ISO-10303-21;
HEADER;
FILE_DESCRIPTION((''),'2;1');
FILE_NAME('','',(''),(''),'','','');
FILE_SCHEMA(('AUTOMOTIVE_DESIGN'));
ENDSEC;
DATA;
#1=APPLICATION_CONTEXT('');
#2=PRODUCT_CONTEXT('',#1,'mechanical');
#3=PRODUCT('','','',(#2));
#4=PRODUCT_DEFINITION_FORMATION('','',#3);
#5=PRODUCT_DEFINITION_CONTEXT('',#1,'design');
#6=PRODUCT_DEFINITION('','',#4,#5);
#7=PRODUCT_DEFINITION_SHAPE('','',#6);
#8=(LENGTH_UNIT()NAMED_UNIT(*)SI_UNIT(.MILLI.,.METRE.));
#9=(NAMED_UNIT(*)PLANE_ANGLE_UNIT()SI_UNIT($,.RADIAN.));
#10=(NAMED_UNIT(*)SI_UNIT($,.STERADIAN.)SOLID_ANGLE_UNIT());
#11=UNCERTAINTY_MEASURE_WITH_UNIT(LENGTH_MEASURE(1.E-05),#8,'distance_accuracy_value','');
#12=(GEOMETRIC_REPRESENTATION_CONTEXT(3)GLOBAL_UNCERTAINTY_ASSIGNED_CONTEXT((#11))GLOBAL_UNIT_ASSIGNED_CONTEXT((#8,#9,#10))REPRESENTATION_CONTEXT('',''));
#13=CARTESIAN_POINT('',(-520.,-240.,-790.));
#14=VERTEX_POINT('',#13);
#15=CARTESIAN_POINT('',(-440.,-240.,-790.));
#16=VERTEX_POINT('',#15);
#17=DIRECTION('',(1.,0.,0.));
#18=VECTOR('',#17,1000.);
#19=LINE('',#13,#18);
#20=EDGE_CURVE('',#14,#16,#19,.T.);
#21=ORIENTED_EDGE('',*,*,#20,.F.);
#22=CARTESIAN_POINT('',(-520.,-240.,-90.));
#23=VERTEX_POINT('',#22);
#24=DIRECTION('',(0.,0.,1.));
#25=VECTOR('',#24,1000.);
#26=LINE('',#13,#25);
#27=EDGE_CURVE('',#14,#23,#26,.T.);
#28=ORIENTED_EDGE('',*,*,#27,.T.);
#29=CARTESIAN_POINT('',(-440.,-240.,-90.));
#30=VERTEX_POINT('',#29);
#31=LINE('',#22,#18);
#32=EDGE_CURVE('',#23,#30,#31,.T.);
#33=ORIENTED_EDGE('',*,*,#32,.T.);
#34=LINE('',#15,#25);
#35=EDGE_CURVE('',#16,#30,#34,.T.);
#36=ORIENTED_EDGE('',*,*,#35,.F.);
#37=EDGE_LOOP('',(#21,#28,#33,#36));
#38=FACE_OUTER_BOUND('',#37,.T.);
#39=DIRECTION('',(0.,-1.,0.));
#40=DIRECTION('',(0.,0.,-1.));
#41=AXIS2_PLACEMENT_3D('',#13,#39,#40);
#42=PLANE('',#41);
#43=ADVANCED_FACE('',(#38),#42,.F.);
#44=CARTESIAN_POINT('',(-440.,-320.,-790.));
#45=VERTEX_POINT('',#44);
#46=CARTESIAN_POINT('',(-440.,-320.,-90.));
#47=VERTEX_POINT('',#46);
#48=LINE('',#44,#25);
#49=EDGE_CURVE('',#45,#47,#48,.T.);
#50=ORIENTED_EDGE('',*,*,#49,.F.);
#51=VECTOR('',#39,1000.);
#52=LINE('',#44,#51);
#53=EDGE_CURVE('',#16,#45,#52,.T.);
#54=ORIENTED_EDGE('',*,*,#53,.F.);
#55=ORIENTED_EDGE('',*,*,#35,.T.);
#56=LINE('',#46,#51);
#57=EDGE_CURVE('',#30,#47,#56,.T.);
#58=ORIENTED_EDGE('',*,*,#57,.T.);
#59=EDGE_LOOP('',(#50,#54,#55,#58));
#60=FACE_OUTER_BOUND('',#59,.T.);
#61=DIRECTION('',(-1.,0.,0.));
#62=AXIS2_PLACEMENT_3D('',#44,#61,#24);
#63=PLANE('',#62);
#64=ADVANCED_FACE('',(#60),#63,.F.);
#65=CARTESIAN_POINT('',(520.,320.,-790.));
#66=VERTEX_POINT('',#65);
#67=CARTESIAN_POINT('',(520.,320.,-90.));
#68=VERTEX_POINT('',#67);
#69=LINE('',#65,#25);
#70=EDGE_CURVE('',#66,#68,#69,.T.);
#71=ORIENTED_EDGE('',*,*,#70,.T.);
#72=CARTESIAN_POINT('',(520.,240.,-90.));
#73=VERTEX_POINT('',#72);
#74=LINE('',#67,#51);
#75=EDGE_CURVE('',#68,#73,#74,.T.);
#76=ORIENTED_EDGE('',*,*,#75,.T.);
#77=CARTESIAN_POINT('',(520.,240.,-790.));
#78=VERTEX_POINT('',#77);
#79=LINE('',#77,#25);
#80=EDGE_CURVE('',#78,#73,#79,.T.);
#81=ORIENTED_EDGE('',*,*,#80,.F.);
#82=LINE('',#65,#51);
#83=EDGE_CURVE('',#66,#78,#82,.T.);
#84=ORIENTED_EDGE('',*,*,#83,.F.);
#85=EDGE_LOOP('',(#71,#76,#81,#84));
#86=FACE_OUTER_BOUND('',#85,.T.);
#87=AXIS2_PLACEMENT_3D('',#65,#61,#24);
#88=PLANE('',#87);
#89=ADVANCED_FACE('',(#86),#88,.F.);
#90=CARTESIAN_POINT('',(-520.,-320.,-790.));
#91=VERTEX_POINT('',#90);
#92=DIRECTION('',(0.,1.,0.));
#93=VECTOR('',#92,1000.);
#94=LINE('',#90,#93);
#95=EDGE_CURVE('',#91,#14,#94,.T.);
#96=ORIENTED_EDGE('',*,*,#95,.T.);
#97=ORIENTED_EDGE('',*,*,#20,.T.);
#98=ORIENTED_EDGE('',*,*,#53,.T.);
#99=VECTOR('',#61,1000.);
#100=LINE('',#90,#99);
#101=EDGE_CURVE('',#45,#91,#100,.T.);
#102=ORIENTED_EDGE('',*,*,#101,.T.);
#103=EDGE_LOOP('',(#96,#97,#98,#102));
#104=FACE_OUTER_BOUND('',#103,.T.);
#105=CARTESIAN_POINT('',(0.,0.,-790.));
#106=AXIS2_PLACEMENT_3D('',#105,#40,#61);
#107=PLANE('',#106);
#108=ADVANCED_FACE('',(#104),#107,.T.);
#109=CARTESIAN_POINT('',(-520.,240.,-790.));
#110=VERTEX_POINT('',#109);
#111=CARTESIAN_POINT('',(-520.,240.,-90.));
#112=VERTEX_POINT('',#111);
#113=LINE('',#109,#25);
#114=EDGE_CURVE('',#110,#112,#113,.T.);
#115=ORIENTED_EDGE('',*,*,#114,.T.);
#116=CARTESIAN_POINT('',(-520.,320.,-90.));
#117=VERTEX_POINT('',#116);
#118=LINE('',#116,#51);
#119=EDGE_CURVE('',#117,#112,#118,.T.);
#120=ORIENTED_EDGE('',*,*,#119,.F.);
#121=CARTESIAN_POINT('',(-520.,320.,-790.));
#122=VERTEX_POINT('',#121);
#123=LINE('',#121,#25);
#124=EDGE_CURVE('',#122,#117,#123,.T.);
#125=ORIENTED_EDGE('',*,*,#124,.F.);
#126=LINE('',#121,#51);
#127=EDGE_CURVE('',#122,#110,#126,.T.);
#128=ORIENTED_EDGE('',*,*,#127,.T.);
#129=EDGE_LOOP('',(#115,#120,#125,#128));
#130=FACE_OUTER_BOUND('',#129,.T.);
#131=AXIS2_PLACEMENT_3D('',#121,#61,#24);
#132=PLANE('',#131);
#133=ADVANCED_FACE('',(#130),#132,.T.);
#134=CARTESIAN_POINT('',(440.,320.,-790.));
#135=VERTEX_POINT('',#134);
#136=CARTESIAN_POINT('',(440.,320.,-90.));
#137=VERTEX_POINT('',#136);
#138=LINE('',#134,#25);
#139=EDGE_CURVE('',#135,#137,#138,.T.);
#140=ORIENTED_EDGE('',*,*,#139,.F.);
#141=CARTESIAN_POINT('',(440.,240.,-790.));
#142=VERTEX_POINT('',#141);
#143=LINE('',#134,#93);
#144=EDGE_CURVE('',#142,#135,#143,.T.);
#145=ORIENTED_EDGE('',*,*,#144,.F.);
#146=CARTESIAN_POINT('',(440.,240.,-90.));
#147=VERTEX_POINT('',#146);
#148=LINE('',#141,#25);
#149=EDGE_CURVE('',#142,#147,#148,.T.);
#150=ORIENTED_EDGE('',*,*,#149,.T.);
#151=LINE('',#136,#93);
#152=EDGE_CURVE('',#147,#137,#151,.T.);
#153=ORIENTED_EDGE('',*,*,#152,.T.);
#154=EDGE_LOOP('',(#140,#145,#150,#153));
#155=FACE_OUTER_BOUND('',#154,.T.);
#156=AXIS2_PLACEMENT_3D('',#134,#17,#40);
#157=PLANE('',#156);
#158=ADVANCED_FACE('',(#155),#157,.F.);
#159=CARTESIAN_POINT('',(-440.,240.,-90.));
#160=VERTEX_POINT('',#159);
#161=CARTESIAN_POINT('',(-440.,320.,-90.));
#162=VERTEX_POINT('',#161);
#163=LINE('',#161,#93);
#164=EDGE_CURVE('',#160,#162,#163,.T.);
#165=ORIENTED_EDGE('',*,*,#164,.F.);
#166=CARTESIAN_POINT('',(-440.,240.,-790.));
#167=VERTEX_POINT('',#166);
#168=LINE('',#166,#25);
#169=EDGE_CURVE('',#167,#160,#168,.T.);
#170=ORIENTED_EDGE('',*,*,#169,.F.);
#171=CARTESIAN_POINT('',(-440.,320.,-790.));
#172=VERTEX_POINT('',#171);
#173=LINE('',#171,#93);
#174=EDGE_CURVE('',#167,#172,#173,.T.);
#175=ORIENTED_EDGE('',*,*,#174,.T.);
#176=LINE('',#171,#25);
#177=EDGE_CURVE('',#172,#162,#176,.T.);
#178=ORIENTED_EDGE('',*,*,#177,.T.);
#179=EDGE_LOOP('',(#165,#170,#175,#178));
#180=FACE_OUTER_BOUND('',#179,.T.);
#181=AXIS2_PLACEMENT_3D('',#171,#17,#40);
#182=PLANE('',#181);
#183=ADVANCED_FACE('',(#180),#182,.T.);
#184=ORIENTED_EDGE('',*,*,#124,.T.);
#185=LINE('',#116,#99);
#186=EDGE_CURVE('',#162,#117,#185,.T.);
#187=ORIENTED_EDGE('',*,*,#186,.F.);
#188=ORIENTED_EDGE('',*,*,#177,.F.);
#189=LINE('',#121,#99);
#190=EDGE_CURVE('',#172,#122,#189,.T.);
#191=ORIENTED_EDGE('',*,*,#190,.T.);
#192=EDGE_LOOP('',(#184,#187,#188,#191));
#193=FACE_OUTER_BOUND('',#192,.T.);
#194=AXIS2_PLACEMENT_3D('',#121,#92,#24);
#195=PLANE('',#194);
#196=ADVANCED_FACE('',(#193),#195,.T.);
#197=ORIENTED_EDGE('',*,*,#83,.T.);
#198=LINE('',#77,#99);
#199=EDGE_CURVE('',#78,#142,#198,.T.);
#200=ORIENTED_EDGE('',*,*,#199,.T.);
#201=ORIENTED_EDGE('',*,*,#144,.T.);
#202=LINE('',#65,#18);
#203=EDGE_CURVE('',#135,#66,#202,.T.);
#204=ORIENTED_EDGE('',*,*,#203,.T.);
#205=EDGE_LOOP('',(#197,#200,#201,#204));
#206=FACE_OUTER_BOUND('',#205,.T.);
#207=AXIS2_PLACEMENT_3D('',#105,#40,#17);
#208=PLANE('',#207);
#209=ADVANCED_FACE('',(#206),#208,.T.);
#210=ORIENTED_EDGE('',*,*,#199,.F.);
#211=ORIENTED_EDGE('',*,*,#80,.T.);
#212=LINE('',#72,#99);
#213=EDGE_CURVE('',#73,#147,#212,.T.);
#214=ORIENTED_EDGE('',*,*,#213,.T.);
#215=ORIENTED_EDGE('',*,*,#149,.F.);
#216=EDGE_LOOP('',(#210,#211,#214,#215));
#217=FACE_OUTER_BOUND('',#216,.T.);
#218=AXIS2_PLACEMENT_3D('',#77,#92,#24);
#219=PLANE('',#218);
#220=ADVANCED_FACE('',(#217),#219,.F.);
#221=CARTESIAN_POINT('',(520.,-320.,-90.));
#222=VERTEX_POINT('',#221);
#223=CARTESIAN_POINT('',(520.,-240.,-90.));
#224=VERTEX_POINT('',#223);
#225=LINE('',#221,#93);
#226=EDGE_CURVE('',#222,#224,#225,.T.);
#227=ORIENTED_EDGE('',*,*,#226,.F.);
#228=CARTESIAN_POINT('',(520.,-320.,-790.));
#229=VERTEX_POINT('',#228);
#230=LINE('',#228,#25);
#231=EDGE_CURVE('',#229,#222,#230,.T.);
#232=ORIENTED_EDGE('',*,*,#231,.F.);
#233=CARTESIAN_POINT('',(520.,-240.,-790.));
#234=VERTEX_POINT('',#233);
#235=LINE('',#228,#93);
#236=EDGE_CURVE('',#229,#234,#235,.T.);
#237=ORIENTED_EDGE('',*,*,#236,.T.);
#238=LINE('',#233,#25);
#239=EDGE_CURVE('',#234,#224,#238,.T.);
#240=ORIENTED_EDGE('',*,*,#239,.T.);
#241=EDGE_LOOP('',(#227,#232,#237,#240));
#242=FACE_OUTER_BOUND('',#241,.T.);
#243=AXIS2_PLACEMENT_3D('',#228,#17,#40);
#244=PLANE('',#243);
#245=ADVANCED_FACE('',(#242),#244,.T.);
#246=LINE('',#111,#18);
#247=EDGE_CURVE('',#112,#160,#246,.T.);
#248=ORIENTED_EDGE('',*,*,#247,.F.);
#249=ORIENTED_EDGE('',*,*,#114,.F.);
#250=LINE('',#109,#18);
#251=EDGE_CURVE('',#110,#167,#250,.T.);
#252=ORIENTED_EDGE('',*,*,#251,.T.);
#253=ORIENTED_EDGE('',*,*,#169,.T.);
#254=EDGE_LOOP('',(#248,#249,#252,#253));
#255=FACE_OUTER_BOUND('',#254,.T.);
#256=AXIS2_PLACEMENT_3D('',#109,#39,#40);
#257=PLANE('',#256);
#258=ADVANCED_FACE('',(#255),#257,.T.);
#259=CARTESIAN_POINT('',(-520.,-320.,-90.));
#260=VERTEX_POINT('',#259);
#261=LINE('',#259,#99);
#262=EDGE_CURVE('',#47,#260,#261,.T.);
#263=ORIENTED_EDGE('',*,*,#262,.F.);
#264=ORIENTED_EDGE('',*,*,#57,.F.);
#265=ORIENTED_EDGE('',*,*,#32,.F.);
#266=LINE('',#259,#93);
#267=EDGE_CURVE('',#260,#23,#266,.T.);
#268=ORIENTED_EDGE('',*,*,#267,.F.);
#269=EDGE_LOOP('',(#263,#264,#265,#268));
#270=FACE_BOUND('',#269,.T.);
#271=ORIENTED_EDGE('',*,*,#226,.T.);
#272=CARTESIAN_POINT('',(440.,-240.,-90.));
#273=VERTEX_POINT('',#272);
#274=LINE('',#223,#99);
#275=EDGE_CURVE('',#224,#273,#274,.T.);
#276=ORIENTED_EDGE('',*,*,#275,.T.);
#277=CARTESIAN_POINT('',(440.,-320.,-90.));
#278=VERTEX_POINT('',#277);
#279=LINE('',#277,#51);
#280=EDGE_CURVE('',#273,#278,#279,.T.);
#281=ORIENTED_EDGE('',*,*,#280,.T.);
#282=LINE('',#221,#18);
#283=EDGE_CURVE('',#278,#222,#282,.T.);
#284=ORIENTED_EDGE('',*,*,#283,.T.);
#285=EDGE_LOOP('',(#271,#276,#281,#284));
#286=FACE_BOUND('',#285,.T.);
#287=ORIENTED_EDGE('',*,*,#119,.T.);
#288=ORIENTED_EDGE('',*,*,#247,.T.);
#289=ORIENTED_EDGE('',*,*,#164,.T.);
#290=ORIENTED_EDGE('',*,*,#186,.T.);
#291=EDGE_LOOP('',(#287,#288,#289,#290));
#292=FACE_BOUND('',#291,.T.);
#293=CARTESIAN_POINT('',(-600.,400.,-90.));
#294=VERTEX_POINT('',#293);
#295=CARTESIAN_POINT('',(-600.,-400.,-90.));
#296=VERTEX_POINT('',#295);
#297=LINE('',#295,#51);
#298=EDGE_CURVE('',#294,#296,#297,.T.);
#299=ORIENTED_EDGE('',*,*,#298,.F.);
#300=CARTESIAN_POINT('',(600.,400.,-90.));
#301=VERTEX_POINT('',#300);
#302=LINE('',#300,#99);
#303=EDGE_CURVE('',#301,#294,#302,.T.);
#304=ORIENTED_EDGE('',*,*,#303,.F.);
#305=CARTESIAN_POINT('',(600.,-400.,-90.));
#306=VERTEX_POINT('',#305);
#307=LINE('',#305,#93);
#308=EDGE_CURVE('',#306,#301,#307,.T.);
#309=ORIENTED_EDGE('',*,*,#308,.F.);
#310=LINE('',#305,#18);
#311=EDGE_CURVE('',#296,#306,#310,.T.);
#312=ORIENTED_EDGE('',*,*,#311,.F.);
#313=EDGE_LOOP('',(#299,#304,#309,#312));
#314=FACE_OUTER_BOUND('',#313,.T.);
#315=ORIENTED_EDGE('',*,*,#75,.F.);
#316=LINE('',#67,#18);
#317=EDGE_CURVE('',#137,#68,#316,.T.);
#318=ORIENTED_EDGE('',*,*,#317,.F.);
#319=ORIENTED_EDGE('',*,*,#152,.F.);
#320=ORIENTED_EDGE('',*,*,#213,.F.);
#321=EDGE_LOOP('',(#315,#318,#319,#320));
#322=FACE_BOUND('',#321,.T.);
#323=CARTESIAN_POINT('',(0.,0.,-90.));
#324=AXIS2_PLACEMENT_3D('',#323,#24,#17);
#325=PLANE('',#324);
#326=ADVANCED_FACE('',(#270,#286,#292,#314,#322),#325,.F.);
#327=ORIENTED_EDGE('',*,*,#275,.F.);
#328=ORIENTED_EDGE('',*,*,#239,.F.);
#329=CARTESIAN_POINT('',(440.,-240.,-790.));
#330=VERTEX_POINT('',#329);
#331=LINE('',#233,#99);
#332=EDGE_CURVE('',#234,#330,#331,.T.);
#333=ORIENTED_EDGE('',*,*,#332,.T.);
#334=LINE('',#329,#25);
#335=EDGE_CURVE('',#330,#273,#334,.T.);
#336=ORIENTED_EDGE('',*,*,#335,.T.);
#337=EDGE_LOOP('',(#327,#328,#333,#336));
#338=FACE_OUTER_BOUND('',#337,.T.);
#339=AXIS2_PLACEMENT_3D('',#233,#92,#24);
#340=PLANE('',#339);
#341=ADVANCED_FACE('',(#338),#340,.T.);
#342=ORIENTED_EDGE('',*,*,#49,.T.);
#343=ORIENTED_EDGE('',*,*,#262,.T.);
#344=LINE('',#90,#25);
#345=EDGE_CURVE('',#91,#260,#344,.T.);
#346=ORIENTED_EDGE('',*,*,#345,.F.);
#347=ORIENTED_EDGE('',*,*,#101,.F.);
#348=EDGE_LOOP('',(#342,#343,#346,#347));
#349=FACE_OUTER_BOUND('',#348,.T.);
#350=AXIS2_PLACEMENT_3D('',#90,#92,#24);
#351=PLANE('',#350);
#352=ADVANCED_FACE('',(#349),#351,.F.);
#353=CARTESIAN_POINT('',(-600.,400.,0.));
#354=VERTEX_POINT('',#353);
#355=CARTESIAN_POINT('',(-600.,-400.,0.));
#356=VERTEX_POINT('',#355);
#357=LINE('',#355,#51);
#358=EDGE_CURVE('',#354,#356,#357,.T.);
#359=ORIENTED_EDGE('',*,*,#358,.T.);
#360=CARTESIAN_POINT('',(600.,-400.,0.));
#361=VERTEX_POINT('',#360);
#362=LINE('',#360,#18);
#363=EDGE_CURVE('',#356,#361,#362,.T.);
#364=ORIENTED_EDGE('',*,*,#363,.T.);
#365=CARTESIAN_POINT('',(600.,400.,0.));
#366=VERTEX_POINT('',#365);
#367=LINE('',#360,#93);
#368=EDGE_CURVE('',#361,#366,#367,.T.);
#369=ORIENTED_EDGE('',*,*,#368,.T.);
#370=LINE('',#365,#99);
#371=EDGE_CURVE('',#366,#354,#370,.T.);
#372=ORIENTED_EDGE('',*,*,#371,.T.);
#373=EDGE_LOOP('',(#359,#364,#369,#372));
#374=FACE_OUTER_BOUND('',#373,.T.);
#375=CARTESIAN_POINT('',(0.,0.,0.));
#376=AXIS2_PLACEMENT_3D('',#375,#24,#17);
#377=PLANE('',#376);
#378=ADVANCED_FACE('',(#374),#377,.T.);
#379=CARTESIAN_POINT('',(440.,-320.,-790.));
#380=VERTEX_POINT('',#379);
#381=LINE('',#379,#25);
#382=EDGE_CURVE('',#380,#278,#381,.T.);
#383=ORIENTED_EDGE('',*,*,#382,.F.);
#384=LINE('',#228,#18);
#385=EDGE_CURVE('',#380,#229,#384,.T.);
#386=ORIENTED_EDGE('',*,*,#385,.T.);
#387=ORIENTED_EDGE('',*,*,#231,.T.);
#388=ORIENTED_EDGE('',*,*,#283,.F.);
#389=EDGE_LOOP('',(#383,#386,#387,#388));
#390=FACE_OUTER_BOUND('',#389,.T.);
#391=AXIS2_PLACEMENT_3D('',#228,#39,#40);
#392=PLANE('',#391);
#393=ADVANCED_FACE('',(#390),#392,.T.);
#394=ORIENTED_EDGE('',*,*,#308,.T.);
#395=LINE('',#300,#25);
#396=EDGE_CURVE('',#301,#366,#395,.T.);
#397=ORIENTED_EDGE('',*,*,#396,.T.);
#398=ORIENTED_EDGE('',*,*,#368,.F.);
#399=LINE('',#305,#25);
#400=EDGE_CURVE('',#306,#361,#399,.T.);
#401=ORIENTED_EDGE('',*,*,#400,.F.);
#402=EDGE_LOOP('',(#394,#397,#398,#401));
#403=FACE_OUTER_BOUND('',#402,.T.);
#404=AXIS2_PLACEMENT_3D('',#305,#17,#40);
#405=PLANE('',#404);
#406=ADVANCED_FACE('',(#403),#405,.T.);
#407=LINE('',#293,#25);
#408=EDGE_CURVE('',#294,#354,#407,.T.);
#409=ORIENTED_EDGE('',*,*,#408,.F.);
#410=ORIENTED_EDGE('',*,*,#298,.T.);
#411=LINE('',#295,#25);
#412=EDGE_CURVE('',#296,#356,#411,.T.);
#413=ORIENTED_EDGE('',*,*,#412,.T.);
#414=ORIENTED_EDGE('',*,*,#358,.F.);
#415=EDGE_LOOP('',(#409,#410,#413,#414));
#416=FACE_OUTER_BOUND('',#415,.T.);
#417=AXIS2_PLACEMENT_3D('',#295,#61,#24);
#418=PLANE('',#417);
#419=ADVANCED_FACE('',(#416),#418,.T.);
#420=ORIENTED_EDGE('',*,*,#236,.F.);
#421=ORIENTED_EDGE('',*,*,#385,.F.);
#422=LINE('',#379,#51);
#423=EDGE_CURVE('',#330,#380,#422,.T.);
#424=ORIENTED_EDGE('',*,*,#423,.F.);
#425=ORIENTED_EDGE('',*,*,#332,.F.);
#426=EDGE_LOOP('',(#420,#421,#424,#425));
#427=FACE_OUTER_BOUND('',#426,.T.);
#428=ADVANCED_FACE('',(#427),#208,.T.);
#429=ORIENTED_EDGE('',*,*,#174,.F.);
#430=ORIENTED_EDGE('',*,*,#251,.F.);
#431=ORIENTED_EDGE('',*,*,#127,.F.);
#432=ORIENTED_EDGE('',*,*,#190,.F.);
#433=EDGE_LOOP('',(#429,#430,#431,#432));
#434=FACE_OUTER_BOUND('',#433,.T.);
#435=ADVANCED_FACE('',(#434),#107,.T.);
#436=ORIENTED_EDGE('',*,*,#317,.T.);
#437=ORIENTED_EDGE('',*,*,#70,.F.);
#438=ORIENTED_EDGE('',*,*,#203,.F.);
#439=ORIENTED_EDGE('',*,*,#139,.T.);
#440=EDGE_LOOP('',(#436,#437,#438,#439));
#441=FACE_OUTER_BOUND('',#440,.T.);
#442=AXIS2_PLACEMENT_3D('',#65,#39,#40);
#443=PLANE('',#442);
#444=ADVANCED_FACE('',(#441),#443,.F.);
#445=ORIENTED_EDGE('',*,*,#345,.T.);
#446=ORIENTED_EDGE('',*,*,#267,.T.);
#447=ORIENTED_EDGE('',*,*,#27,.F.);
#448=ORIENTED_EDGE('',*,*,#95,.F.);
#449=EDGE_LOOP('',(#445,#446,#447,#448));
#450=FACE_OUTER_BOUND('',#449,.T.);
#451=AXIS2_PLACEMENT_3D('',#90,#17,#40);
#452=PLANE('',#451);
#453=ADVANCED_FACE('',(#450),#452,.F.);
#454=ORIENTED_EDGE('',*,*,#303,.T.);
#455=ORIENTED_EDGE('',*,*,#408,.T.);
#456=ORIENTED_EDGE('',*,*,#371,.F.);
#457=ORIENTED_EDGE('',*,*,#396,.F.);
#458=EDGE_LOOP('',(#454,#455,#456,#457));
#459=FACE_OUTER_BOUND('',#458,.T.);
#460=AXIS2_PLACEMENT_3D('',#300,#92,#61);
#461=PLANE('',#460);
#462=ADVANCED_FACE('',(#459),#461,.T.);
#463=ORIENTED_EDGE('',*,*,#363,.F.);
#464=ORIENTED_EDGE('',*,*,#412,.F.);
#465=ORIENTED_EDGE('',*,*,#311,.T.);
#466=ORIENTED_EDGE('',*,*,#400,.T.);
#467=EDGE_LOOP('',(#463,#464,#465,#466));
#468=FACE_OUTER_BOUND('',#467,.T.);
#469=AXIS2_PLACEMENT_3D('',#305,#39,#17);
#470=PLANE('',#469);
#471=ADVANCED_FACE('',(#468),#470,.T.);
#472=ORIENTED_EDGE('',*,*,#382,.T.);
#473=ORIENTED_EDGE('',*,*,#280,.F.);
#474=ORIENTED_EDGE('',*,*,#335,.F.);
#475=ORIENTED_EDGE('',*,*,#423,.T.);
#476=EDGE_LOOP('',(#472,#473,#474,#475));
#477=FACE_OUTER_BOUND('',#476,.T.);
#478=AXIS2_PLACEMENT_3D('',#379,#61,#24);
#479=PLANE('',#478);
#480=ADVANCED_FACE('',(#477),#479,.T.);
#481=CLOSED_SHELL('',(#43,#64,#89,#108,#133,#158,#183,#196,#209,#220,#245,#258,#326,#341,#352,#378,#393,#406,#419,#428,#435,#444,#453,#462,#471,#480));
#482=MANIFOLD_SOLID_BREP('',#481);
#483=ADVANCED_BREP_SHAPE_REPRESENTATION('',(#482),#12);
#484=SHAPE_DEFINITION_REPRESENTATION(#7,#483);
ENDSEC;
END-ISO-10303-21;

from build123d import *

# Parameters (mm, degrees)
SKETCH1_W               = 1200
SKETCH1_H               = 800
BOSS_EXTRUDE1_DEPTH     = 90
SKETCH2_W               = 80
SKETCH2_H               = 80
BOSS_EXTRUDE2_DEPTH     = 700
MIRROR2_COPY_1_SKETCH_W = 80
MIRROR2_COPY_1_SKETCH_H = 80
MIRROR2_COPY_1_DEPTH    = 700


with BuildPart() as part:
    # Sketch1 → Boss-Extrude1 (new body)
    with BuildSketch(Plane.XY):
        Rectangle(SKETCH1_W, SKETCH1_H)
    extrude(amount=-BOSS_EXTRUDE1_DEPTH)

    # Sketch2 → Boss-Extrude2 (add)
    with BuildSketch(Plane(origin=(0, 0, -90), x_dir=(-1, 0, 0), z_dir=(0, 0, -1))):
        with Locations((480, -280)):
            Rectangle(SKETCH2_W, SKETCH2_H)
    boss_extrude2 = extrude(amount=BOSS_EXTRUDE2_DEPTH)

    # Mirror1: Boss-Extrude2 across plane
    add(boss_extrude2.mirror(Plane.ZX))

    # Mirror2: Boss-Extrude2 across plane
    add(boss_extrude2.mirror(Plane(origin=(0, 0, 0), x_dir=(0, 0, 1), z_dir=(1, 0, 0))))

    # Mirror2 copy 1 sketch → Mirror2 copy 1 (add)
    with BuildSketch(Plane(origin=(0, 0, -90), x_dir=(1, 0, 0), z_dir=(0, 0, -1))):
        with Locations((480, -280)):
            Rectangle(MIRROR2_COPY_1_SKETCH_W, MIRROR2_COPY_1_SKETCH_H)
    extrude(amount=MIRROR2_COPY_1_DEPTH)


solid = part.part
